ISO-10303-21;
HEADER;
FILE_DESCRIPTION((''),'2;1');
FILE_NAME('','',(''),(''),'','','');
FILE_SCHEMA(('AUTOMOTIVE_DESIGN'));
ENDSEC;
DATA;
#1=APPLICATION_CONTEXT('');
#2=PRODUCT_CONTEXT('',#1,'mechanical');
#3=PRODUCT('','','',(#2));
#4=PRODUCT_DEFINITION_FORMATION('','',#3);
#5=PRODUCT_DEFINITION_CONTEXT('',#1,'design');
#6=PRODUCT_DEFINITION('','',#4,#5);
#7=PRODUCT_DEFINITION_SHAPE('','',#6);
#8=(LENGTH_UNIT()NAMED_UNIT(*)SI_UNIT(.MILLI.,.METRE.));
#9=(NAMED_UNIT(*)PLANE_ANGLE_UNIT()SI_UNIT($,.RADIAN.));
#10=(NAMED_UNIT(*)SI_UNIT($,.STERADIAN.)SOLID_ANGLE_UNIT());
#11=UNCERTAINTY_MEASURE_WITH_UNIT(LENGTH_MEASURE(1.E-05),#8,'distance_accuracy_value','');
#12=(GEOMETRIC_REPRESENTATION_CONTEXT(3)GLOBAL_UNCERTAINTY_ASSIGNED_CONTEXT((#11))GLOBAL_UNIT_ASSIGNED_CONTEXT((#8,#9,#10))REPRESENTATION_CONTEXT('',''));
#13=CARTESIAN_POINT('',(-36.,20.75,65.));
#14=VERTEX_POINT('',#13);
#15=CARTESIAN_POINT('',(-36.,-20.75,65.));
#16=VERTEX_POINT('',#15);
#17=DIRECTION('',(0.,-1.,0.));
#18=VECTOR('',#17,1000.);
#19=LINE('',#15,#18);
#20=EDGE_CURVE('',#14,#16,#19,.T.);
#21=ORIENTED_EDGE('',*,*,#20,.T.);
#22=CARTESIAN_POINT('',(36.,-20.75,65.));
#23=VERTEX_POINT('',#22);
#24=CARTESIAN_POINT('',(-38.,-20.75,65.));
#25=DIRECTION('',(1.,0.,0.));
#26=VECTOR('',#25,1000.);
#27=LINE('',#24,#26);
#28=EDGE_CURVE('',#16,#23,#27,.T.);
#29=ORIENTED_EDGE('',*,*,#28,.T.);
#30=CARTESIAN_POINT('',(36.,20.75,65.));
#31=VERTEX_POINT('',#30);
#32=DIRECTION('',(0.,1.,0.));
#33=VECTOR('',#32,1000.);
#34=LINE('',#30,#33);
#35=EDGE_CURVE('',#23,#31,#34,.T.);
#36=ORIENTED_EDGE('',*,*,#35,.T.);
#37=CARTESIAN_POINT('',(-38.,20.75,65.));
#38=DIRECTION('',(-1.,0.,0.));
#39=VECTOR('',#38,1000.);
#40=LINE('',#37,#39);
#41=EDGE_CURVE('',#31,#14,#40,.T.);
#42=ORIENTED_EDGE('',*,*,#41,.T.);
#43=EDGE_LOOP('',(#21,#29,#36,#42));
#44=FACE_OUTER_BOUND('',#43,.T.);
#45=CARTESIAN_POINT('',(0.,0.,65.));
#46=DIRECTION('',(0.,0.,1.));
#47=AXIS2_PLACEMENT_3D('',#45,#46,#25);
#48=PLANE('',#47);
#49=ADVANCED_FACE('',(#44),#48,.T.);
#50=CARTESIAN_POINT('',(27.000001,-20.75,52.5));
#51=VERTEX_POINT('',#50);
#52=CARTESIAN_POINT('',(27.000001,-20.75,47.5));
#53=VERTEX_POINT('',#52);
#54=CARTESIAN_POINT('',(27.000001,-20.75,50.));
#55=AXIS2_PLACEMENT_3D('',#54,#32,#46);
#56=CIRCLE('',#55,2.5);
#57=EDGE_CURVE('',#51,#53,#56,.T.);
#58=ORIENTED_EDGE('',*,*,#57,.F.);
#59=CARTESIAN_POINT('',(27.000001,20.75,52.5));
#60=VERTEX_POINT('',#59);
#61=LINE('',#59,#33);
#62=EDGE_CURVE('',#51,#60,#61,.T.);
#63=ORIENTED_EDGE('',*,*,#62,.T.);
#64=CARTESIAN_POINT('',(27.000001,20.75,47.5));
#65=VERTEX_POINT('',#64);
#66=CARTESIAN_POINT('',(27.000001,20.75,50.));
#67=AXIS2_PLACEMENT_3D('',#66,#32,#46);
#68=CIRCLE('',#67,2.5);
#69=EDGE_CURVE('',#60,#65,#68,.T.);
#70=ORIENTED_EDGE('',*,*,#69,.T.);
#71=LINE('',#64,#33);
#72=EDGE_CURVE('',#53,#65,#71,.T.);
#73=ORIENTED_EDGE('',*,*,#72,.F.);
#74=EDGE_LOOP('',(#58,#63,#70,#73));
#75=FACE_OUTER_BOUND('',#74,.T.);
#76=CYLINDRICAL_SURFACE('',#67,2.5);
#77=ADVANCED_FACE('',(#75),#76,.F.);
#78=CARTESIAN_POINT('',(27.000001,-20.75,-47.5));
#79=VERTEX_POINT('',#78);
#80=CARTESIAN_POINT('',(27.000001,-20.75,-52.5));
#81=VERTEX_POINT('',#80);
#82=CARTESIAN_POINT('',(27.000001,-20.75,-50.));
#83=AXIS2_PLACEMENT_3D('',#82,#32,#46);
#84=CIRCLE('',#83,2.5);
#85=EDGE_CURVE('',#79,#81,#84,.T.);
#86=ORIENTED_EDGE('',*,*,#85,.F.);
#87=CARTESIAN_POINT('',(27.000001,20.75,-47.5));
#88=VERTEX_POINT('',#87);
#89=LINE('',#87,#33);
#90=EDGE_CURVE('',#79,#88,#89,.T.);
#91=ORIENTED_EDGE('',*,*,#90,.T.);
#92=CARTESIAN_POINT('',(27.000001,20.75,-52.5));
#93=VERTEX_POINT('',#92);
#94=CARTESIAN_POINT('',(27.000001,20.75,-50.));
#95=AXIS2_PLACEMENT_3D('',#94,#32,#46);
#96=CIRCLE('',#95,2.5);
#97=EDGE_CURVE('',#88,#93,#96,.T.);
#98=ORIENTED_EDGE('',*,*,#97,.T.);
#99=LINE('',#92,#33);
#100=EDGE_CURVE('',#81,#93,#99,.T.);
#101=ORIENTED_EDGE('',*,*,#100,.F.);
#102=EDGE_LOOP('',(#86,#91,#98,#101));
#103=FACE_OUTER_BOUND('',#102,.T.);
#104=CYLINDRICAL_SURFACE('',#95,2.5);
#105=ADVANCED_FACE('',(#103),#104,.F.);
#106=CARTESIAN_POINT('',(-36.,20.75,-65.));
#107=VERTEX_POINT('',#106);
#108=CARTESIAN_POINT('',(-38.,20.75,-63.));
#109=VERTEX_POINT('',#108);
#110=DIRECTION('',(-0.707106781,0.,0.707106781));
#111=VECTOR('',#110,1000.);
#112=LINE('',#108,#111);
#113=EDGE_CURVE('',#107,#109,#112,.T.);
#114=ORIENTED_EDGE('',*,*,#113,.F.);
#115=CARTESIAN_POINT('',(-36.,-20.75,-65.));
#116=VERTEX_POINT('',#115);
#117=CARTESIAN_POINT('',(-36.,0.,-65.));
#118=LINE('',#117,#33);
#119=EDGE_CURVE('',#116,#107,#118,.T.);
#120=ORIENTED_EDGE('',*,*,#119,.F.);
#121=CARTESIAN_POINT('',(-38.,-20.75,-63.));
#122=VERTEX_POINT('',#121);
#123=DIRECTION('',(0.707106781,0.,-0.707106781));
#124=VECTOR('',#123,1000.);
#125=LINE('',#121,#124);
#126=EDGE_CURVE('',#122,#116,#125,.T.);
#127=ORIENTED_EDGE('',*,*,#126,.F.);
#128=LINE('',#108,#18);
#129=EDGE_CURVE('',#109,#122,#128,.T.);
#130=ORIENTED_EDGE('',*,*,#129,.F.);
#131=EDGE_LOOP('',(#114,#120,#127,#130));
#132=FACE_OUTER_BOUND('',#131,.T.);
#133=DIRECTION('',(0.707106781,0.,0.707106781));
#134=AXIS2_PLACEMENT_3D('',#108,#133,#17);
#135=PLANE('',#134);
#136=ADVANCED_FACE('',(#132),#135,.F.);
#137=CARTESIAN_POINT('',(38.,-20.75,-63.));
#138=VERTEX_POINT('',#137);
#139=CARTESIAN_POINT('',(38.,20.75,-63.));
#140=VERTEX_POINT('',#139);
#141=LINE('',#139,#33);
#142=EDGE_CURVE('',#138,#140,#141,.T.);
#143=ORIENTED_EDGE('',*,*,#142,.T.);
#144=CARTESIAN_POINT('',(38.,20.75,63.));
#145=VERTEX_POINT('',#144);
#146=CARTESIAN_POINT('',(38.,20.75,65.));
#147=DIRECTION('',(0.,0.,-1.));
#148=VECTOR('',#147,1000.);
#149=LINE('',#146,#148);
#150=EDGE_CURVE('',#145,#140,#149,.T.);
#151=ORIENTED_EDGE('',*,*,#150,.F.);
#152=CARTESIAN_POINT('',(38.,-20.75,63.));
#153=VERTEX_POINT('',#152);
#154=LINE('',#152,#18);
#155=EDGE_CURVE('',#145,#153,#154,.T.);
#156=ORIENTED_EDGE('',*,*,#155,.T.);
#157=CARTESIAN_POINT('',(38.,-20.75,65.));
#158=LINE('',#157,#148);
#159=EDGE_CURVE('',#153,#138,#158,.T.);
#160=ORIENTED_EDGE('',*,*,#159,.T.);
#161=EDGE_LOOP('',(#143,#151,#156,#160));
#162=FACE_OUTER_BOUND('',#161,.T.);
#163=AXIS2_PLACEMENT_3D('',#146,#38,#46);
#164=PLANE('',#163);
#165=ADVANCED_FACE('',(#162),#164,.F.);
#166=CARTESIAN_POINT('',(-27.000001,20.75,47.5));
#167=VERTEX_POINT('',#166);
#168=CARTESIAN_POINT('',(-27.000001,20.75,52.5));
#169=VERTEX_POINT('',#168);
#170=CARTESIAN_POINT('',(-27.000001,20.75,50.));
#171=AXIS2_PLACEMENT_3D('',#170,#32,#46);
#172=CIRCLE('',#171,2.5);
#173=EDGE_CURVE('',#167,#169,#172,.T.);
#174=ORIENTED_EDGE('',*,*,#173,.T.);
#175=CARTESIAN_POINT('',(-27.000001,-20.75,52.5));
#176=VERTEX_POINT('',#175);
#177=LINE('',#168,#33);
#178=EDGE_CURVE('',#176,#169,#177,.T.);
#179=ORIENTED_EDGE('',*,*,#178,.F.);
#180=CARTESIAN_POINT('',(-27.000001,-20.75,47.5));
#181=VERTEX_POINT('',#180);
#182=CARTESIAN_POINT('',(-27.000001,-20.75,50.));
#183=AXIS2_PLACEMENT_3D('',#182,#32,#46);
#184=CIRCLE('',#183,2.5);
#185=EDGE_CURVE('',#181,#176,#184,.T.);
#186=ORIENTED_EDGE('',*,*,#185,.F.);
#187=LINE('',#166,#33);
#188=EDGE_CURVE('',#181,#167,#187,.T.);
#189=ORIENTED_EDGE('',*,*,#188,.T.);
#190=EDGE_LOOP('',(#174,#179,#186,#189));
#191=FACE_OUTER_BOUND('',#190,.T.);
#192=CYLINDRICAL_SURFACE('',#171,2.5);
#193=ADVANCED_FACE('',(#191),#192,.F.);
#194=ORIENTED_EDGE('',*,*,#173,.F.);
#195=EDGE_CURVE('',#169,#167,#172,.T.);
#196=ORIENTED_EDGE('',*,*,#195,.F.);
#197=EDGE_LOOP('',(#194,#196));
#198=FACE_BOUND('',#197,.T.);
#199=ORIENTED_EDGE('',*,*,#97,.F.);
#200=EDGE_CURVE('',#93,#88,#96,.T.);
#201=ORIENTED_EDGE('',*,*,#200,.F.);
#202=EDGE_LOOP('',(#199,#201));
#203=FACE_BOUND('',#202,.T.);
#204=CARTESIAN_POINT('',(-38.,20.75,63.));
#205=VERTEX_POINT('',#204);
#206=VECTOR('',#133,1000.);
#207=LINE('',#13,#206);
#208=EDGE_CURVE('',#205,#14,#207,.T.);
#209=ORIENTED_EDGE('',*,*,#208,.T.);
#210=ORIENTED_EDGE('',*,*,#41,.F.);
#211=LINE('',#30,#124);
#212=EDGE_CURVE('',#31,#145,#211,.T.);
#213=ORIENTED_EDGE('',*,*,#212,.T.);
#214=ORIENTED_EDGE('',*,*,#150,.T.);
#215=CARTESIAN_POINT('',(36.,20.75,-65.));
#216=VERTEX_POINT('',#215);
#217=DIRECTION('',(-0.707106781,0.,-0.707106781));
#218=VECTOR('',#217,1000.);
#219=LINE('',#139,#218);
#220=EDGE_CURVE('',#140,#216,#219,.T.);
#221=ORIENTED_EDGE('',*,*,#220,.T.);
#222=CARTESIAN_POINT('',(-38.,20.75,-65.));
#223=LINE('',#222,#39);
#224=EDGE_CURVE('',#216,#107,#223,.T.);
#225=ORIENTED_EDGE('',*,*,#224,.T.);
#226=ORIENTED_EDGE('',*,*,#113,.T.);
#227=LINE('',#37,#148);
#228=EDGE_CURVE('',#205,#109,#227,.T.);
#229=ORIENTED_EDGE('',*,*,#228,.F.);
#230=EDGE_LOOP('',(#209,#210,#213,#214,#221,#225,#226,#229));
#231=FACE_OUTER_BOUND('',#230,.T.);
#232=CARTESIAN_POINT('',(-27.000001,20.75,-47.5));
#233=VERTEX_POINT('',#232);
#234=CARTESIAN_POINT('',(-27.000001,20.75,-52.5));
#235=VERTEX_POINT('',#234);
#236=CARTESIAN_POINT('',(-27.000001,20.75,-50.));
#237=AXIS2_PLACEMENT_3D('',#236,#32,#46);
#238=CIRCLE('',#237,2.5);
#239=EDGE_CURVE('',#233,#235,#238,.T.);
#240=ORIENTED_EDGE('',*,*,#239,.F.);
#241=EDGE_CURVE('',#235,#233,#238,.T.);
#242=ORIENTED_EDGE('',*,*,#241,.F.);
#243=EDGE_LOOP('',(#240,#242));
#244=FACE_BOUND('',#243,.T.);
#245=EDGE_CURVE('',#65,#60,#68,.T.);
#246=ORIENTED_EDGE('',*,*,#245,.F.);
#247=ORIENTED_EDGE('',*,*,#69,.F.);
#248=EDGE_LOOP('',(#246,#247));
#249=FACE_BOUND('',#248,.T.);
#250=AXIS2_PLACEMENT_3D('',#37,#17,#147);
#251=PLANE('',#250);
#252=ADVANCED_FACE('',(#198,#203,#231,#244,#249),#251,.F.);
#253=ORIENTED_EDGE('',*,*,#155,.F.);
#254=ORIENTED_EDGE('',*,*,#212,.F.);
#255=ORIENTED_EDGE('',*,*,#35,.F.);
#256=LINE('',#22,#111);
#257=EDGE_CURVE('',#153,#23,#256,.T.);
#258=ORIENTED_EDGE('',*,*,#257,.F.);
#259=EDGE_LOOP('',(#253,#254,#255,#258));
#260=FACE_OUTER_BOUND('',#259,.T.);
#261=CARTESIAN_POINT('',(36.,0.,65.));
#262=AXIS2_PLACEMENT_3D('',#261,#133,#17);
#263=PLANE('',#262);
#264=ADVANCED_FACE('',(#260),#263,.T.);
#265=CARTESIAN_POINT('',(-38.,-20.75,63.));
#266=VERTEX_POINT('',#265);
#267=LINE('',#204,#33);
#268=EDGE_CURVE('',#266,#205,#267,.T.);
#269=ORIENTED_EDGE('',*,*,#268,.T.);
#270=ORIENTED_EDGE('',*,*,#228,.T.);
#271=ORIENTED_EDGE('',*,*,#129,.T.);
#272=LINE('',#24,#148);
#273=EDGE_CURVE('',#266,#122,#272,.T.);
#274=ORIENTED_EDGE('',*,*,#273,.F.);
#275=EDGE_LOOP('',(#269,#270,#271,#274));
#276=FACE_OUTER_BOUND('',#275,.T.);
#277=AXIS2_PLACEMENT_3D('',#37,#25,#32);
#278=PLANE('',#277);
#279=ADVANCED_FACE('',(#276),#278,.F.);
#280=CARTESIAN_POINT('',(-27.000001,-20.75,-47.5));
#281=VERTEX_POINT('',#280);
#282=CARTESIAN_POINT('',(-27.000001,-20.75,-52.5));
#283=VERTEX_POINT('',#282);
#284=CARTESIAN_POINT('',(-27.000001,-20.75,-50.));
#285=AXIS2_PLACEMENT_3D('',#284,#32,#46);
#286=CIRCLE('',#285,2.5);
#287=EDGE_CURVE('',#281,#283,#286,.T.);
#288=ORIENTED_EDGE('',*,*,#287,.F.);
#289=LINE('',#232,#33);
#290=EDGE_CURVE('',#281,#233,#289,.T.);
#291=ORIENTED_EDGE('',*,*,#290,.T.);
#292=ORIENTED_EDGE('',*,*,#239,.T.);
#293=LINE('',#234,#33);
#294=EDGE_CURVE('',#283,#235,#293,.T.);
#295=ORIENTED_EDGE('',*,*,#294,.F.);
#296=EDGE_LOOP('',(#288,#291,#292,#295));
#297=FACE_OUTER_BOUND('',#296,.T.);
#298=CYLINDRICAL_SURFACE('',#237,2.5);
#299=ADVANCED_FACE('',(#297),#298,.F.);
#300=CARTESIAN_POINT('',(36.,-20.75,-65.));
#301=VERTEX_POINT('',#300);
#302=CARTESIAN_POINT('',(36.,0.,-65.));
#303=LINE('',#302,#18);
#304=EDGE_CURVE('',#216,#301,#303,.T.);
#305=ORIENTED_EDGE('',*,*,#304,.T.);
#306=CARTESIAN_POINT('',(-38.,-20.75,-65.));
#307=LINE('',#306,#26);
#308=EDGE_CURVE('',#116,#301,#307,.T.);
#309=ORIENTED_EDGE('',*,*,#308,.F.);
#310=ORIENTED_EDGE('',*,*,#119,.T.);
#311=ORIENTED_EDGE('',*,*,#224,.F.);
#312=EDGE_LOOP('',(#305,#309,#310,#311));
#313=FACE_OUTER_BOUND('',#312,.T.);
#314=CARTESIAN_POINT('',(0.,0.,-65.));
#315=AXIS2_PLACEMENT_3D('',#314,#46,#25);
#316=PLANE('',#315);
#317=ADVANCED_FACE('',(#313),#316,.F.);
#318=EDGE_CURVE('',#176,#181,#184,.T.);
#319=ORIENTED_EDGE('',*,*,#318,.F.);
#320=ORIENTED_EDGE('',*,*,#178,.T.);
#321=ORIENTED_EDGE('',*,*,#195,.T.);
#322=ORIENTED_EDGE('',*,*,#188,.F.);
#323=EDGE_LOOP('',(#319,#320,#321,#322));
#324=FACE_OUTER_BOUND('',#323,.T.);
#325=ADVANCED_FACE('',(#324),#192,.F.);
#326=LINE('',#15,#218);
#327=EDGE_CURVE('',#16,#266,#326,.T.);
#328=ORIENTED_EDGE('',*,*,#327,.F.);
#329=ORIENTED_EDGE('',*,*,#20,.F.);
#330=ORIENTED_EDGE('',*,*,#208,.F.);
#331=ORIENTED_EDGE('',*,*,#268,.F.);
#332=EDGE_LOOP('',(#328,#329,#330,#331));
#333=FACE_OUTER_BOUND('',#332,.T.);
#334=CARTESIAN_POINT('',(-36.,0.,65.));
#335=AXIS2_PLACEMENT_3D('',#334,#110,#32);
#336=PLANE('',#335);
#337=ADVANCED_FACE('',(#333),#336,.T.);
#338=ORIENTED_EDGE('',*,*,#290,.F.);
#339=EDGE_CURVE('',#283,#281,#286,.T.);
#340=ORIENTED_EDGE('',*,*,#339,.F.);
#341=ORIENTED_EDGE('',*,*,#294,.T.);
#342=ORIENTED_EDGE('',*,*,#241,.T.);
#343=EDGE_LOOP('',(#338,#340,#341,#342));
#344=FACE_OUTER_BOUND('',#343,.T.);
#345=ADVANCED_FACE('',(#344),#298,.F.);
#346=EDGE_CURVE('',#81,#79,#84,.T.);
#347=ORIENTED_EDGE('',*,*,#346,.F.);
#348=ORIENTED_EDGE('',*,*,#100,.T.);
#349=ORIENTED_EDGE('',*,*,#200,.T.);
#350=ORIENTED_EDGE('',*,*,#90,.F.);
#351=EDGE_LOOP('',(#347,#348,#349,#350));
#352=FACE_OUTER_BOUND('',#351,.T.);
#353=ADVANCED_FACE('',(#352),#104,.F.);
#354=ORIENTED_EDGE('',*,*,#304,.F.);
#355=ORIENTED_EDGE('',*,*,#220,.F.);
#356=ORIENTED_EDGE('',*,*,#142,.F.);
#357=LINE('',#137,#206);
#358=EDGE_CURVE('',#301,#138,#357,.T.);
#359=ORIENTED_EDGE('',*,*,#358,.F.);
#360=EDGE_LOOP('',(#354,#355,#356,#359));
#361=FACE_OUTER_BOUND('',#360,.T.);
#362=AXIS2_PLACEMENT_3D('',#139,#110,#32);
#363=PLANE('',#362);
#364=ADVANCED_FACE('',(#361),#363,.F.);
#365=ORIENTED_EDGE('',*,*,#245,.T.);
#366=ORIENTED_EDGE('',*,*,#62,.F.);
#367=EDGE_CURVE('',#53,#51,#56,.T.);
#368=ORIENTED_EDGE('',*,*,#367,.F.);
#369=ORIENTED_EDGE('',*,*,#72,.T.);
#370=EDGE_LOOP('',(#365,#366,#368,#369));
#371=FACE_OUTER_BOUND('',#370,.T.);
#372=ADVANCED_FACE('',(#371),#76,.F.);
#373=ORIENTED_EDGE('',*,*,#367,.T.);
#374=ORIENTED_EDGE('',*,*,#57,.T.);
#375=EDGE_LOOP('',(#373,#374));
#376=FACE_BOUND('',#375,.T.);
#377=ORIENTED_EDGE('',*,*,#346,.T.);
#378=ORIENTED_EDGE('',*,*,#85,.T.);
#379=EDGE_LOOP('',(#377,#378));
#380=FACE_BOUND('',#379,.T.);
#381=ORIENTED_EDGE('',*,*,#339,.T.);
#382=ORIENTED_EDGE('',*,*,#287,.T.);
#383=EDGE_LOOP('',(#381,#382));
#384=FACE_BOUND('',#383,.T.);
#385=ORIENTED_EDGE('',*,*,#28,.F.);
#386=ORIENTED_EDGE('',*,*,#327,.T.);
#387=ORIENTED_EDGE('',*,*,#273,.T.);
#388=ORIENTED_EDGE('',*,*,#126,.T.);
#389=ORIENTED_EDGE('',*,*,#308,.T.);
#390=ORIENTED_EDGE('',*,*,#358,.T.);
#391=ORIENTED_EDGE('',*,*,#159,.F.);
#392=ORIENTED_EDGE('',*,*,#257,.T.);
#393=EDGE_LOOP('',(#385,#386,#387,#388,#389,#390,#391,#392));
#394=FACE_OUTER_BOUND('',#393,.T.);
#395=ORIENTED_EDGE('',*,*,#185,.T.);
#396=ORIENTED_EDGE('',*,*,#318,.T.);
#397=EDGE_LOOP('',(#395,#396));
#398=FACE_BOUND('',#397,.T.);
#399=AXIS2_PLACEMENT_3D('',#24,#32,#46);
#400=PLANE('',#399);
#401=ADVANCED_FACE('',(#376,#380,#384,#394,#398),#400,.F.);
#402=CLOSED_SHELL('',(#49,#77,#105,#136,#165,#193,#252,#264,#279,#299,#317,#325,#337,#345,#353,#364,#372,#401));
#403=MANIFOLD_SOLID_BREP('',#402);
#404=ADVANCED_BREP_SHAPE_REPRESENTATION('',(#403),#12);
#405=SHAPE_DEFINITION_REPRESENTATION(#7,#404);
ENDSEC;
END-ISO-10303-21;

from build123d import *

# Parameters (mm, degrees)
SKETCH_1_W         = 76
SKETCH_1_H         = 41.5
EXTRUDE_1_DEPTH    = 65
HOLE_WIZARD_M6_1_D = 5
CHAMFER_1_SIZE     = 2


with BuildPart() as part:
    # 草图1 → 凸台-拉伸1 (new, symmetric)
    with BuildSketch(Plane.XY):
        Rectangle(SKETCH_1_W, SKETCH_1_H)
    extrude(amount=EXTRUDE_1_DEPTH, both=True)

    # M6 螺纹孔1 (through all)
    with Locations(Plane(origin=(0, 20.75, 0), x_dir=(1, 0, 0), z_dir=(0, 1, 0))):
        with Locations((-27.000001035, -50), (27.000001035, -50), (27.000001035, 50), (-27.000001035, 50)):
            Hole(HOLE_WIZARD_M6_1_D / 2)

    # 倒角1
    chamfer_1_edges = [part.edges().sort_by_distance(p)[0] for p in [
        (-38, 0, 65),
        (38, 0, 65),
        (-38, 0, -65),
        (38, 0, -65),
    ]]
    chamfer(chamfer_1_edges, length=CHAMFER_1_SIZE)


solid = part.part
